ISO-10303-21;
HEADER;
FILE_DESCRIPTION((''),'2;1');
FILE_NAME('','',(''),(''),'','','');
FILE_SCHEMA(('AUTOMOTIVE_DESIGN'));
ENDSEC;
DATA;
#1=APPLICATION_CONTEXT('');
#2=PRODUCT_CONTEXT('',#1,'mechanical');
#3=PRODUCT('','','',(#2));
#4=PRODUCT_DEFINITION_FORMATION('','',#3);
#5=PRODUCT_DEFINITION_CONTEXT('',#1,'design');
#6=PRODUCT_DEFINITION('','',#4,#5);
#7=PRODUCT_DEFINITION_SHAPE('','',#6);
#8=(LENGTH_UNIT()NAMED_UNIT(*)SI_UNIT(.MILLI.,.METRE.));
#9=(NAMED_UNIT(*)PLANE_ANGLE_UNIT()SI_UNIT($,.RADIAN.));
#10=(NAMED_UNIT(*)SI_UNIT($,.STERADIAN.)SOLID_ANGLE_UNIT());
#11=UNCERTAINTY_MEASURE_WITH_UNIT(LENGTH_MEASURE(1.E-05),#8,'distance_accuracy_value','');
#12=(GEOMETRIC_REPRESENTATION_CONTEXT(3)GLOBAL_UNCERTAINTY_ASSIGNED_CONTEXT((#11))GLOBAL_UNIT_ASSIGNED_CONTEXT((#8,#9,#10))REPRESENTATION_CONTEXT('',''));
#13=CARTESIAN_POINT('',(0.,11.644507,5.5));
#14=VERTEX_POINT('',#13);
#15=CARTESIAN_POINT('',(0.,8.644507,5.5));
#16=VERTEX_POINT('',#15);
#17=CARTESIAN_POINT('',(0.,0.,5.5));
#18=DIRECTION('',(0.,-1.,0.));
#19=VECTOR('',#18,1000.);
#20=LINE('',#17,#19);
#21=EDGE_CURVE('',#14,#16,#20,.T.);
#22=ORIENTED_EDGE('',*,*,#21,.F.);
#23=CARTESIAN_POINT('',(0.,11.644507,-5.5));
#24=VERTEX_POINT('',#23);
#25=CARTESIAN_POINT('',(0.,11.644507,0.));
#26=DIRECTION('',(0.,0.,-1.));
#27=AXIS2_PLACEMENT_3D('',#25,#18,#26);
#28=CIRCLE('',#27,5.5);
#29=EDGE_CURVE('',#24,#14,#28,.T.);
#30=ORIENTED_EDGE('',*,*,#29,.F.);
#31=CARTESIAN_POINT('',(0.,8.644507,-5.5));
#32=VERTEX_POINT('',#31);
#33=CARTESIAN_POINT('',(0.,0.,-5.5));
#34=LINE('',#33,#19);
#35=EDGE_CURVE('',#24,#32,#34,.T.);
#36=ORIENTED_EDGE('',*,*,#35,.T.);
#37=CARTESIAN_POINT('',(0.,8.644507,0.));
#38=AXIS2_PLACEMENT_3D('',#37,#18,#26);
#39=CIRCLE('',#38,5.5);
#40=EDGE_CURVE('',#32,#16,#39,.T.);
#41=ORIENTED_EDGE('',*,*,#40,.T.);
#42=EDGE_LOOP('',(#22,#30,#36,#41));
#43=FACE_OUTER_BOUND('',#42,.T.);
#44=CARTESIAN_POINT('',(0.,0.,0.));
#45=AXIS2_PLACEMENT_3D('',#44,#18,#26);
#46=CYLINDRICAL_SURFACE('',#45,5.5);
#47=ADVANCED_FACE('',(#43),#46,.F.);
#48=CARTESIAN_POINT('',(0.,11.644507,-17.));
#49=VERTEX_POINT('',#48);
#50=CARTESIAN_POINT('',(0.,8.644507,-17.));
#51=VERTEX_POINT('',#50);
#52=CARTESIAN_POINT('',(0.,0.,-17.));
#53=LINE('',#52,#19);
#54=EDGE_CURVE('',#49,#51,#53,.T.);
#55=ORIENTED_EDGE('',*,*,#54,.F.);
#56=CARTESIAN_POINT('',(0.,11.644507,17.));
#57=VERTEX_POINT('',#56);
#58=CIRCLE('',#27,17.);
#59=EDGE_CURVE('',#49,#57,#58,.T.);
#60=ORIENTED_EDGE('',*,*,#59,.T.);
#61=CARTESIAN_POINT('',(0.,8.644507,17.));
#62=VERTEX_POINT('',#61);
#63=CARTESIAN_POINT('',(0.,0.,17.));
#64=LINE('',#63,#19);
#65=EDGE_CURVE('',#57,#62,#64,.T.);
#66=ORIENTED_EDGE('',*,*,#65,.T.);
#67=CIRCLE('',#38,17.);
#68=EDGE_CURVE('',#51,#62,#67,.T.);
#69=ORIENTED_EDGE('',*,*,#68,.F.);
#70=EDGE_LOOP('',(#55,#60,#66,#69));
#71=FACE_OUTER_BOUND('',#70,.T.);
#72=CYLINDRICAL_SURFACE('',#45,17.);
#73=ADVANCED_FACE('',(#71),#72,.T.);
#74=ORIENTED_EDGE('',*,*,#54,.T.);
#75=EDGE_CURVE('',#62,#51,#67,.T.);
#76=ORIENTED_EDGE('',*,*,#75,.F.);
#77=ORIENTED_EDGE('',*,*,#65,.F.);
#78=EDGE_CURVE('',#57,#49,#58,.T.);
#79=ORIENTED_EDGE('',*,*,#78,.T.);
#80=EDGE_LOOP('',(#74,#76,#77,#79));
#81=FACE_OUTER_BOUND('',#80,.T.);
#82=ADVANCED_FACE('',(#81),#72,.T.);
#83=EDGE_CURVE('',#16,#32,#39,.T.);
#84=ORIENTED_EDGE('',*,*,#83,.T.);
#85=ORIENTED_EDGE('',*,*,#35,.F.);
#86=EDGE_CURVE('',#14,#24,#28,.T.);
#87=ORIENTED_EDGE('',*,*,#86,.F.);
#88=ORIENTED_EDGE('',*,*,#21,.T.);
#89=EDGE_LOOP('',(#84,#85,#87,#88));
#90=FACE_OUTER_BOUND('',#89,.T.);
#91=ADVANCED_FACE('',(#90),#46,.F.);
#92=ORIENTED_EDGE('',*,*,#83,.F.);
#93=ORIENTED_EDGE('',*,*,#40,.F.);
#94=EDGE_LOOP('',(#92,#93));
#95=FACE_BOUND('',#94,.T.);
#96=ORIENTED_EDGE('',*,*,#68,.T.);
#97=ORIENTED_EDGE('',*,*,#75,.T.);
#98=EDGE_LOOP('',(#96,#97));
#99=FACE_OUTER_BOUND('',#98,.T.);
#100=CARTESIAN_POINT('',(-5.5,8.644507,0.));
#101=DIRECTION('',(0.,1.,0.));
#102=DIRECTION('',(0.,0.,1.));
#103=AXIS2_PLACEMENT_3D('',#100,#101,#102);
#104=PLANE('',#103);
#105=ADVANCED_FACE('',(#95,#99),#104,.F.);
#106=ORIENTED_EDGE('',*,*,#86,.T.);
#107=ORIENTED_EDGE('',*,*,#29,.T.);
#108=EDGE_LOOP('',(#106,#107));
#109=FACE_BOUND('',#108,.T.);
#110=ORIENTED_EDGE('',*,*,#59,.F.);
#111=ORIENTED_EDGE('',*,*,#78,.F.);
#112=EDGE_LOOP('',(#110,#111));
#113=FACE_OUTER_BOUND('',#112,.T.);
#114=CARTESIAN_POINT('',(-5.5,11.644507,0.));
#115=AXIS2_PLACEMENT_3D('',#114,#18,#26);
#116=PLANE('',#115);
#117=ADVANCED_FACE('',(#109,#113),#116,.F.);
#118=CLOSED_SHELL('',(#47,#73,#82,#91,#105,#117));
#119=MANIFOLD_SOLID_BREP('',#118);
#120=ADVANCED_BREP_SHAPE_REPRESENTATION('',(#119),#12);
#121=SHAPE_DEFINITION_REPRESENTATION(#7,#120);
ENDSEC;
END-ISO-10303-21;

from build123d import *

# Parameters (mm, degrees)
SKETCH_1_W = 11.5
SKETCH_1_H = 3


with BuildPart() as part:
    # 草图1 → Revolve 468 (revolve)
    with BuildSketch(Plane.XY, mode=Mode.PRIVATE) as revolve_468_sk:
        with Locations((-11.25, 10.144507042)):
            Rectangle(SKETCH_1_W, SKETCH_1_H)
    revolve(revolve_468_sk.sketch.rotate(Axis((0, 0, 0), (0, 1, 0)), 270), axis=Axis((0, 0, 0), (0, 1, 0)))


solid = part.part
